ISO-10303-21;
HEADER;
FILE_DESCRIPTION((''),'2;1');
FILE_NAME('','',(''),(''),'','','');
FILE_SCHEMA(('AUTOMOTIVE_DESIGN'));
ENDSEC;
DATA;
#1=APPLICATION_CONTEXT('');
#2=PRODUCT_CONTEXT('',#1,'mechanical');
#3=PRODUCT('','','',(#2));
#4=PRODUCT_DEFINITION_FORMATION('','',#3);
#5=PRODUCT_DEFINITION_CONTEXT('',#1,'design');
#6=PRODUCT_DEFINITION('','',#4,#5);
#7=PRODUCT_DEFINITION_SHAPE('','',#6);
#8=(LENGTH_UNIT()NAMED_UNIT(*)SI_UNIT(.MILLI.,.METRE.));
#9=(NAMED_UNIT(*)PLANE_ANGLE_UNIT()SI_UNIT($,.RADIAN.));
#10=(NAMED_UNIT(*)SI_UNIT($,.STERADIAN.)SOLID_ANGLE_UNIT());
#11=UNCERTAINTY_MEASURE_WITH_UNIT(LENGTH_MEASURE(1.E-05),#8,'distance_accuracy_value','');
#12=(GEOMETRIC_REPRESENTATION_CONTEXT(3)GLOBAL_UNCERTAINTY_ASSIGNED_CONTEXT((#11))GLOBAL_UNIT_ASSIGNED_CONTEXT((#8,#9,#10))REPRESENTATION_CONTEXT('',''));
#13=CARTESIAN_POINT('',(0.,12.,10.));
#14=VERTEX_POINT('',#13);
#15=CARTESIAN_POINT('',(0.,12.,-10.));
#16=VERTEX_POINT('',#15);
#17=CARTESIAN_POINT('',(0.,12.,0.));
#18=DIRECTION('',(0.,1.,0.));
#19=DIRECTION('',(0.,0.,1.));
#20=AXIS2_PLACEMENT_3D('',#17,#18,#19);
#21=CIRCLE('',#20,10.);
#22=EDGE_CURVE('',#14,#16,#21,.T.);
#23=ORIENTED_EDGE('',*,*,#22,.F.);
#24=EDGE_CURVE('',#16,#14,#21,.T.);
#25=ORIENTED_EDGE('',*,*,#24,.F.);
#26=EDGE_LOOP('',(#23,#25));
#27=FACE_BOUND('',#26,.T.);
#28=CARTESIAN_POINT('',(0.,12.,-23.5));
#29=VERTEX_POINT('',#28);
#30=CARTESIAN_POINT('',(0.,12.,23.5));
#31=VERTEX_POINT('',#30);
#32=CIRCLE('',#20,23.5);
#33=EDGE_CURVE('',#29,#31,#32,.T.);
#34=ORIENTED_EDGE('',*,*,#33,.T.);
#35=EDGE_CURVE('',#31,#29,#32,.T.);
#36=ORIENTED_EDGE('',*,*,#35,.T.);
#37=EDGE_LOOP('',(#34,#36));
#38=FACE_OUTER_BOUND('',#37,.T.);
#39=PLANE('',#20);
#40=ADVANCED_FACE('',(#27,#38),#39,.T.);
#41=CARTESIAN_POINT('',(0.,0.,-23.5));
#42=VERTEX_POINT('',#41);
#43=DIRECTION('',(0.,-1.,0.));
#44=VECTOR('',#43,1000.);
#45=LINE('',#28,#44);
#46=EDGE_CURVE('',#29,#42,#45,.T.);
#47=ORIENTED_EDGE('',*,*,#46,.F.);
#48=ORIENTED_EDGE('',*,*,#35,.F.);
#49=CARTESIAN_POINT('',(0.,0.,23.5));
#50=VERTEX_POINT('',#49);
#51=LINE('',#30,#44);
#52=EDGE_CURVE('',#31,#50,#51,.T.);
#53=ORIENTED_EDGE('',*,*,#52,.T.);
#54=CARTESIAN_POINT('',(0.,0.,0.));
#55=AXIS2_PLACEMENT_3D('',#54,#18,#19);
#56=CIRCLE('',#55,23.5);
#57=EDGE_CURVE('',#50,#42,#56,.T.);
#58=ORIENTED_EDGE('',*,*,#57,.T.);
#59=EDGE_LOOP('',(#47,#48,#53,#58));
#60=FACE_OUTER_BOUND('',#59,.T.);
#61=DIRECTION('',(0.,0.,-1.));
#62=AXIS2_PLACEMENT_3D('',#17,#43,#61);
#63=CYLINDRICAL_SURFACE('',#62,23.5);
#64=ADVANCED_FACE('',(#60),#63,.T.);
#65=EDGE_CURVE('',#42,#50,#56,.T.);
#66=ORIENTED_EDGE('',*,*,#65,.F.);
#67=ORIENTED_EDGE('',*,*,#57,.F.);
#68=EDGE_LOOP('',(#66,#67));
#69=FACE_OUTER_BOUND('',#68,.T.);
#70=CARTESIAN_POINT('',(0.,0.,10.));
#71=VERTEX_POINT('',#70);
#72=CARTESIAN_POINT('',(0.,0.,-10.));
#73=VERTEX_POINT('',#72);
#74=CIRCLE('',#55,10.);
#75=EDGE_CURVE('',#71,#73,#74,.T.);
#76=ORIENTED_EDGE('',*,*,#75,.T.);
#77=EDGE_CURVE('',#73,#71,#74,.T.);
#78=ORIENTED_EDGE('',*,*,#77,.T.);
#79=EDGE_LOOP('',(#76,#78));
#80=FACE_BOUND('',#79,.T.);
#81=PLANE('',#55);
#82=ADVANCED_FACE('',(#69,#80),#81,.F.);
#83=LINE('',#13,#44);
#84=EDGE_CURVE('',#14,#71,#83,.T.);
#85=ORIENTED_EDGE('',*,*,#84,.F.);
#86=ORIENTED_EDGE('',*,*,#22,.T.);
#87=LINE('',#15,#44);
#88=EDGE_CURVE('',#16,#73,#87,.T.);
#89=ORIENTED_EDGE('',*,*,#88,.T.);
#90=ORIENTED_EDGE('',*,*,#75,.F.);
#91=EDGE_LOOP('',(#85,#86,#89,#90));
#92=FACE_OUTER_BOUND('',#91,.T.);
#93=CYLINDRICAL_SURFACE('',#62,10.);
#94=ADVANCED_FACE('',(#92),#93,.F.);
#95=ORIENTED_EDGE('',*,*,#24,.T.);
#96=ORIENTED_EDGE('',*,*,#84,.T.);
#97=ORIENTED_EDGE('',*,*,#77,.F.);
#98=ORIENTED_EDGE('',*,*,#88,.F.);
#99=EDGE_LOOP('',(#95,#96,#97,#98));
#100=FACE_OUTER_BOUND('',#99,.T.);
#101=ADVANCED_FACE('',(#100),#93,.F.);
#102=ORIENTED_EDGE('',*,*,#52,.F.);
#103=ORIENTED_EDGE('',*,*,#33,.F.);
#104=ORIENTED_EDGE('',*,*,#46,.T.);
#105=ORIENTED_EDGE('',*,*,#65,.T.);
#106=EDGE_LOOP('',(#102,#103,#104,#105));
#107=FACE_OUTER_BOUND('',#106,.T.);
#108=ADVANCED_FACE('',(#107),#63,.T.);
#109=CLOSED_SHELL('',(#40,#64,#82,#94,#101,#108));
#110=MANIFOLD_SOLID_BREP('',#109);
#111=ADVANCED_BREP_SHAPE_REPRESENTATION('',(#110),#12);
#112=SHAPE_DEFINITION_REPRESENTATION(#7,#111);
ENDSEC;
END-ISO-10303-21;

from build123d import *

# Parameters (mm, degrees)
SKETCH1_R           = 23.5
SKETCH1_R_2         = 10
BOSS_EXTRUDE1_DEPTH = 12


with BuildPart() as part:
    # Sketch1 → Boss-Extrude1 (new body)
    with BuildSketch(Plane(origin=(0, 0, 0), x_dir=(1, 0, 0), z_dir=(0, 1, 0))):
        with Locations(Location((0, 0, 0), (0, 0, 270))):
            Circle(SKETCH1_R)
        with Locations(Location((0, 0, 0), (0, 0, 270))):
            Circle(SKETCH1_R_2, mode=Mode.SUBTRACT)
    extrude(amount=BOSS_EXTRUDE1_DEPTH)


solid = part.part
